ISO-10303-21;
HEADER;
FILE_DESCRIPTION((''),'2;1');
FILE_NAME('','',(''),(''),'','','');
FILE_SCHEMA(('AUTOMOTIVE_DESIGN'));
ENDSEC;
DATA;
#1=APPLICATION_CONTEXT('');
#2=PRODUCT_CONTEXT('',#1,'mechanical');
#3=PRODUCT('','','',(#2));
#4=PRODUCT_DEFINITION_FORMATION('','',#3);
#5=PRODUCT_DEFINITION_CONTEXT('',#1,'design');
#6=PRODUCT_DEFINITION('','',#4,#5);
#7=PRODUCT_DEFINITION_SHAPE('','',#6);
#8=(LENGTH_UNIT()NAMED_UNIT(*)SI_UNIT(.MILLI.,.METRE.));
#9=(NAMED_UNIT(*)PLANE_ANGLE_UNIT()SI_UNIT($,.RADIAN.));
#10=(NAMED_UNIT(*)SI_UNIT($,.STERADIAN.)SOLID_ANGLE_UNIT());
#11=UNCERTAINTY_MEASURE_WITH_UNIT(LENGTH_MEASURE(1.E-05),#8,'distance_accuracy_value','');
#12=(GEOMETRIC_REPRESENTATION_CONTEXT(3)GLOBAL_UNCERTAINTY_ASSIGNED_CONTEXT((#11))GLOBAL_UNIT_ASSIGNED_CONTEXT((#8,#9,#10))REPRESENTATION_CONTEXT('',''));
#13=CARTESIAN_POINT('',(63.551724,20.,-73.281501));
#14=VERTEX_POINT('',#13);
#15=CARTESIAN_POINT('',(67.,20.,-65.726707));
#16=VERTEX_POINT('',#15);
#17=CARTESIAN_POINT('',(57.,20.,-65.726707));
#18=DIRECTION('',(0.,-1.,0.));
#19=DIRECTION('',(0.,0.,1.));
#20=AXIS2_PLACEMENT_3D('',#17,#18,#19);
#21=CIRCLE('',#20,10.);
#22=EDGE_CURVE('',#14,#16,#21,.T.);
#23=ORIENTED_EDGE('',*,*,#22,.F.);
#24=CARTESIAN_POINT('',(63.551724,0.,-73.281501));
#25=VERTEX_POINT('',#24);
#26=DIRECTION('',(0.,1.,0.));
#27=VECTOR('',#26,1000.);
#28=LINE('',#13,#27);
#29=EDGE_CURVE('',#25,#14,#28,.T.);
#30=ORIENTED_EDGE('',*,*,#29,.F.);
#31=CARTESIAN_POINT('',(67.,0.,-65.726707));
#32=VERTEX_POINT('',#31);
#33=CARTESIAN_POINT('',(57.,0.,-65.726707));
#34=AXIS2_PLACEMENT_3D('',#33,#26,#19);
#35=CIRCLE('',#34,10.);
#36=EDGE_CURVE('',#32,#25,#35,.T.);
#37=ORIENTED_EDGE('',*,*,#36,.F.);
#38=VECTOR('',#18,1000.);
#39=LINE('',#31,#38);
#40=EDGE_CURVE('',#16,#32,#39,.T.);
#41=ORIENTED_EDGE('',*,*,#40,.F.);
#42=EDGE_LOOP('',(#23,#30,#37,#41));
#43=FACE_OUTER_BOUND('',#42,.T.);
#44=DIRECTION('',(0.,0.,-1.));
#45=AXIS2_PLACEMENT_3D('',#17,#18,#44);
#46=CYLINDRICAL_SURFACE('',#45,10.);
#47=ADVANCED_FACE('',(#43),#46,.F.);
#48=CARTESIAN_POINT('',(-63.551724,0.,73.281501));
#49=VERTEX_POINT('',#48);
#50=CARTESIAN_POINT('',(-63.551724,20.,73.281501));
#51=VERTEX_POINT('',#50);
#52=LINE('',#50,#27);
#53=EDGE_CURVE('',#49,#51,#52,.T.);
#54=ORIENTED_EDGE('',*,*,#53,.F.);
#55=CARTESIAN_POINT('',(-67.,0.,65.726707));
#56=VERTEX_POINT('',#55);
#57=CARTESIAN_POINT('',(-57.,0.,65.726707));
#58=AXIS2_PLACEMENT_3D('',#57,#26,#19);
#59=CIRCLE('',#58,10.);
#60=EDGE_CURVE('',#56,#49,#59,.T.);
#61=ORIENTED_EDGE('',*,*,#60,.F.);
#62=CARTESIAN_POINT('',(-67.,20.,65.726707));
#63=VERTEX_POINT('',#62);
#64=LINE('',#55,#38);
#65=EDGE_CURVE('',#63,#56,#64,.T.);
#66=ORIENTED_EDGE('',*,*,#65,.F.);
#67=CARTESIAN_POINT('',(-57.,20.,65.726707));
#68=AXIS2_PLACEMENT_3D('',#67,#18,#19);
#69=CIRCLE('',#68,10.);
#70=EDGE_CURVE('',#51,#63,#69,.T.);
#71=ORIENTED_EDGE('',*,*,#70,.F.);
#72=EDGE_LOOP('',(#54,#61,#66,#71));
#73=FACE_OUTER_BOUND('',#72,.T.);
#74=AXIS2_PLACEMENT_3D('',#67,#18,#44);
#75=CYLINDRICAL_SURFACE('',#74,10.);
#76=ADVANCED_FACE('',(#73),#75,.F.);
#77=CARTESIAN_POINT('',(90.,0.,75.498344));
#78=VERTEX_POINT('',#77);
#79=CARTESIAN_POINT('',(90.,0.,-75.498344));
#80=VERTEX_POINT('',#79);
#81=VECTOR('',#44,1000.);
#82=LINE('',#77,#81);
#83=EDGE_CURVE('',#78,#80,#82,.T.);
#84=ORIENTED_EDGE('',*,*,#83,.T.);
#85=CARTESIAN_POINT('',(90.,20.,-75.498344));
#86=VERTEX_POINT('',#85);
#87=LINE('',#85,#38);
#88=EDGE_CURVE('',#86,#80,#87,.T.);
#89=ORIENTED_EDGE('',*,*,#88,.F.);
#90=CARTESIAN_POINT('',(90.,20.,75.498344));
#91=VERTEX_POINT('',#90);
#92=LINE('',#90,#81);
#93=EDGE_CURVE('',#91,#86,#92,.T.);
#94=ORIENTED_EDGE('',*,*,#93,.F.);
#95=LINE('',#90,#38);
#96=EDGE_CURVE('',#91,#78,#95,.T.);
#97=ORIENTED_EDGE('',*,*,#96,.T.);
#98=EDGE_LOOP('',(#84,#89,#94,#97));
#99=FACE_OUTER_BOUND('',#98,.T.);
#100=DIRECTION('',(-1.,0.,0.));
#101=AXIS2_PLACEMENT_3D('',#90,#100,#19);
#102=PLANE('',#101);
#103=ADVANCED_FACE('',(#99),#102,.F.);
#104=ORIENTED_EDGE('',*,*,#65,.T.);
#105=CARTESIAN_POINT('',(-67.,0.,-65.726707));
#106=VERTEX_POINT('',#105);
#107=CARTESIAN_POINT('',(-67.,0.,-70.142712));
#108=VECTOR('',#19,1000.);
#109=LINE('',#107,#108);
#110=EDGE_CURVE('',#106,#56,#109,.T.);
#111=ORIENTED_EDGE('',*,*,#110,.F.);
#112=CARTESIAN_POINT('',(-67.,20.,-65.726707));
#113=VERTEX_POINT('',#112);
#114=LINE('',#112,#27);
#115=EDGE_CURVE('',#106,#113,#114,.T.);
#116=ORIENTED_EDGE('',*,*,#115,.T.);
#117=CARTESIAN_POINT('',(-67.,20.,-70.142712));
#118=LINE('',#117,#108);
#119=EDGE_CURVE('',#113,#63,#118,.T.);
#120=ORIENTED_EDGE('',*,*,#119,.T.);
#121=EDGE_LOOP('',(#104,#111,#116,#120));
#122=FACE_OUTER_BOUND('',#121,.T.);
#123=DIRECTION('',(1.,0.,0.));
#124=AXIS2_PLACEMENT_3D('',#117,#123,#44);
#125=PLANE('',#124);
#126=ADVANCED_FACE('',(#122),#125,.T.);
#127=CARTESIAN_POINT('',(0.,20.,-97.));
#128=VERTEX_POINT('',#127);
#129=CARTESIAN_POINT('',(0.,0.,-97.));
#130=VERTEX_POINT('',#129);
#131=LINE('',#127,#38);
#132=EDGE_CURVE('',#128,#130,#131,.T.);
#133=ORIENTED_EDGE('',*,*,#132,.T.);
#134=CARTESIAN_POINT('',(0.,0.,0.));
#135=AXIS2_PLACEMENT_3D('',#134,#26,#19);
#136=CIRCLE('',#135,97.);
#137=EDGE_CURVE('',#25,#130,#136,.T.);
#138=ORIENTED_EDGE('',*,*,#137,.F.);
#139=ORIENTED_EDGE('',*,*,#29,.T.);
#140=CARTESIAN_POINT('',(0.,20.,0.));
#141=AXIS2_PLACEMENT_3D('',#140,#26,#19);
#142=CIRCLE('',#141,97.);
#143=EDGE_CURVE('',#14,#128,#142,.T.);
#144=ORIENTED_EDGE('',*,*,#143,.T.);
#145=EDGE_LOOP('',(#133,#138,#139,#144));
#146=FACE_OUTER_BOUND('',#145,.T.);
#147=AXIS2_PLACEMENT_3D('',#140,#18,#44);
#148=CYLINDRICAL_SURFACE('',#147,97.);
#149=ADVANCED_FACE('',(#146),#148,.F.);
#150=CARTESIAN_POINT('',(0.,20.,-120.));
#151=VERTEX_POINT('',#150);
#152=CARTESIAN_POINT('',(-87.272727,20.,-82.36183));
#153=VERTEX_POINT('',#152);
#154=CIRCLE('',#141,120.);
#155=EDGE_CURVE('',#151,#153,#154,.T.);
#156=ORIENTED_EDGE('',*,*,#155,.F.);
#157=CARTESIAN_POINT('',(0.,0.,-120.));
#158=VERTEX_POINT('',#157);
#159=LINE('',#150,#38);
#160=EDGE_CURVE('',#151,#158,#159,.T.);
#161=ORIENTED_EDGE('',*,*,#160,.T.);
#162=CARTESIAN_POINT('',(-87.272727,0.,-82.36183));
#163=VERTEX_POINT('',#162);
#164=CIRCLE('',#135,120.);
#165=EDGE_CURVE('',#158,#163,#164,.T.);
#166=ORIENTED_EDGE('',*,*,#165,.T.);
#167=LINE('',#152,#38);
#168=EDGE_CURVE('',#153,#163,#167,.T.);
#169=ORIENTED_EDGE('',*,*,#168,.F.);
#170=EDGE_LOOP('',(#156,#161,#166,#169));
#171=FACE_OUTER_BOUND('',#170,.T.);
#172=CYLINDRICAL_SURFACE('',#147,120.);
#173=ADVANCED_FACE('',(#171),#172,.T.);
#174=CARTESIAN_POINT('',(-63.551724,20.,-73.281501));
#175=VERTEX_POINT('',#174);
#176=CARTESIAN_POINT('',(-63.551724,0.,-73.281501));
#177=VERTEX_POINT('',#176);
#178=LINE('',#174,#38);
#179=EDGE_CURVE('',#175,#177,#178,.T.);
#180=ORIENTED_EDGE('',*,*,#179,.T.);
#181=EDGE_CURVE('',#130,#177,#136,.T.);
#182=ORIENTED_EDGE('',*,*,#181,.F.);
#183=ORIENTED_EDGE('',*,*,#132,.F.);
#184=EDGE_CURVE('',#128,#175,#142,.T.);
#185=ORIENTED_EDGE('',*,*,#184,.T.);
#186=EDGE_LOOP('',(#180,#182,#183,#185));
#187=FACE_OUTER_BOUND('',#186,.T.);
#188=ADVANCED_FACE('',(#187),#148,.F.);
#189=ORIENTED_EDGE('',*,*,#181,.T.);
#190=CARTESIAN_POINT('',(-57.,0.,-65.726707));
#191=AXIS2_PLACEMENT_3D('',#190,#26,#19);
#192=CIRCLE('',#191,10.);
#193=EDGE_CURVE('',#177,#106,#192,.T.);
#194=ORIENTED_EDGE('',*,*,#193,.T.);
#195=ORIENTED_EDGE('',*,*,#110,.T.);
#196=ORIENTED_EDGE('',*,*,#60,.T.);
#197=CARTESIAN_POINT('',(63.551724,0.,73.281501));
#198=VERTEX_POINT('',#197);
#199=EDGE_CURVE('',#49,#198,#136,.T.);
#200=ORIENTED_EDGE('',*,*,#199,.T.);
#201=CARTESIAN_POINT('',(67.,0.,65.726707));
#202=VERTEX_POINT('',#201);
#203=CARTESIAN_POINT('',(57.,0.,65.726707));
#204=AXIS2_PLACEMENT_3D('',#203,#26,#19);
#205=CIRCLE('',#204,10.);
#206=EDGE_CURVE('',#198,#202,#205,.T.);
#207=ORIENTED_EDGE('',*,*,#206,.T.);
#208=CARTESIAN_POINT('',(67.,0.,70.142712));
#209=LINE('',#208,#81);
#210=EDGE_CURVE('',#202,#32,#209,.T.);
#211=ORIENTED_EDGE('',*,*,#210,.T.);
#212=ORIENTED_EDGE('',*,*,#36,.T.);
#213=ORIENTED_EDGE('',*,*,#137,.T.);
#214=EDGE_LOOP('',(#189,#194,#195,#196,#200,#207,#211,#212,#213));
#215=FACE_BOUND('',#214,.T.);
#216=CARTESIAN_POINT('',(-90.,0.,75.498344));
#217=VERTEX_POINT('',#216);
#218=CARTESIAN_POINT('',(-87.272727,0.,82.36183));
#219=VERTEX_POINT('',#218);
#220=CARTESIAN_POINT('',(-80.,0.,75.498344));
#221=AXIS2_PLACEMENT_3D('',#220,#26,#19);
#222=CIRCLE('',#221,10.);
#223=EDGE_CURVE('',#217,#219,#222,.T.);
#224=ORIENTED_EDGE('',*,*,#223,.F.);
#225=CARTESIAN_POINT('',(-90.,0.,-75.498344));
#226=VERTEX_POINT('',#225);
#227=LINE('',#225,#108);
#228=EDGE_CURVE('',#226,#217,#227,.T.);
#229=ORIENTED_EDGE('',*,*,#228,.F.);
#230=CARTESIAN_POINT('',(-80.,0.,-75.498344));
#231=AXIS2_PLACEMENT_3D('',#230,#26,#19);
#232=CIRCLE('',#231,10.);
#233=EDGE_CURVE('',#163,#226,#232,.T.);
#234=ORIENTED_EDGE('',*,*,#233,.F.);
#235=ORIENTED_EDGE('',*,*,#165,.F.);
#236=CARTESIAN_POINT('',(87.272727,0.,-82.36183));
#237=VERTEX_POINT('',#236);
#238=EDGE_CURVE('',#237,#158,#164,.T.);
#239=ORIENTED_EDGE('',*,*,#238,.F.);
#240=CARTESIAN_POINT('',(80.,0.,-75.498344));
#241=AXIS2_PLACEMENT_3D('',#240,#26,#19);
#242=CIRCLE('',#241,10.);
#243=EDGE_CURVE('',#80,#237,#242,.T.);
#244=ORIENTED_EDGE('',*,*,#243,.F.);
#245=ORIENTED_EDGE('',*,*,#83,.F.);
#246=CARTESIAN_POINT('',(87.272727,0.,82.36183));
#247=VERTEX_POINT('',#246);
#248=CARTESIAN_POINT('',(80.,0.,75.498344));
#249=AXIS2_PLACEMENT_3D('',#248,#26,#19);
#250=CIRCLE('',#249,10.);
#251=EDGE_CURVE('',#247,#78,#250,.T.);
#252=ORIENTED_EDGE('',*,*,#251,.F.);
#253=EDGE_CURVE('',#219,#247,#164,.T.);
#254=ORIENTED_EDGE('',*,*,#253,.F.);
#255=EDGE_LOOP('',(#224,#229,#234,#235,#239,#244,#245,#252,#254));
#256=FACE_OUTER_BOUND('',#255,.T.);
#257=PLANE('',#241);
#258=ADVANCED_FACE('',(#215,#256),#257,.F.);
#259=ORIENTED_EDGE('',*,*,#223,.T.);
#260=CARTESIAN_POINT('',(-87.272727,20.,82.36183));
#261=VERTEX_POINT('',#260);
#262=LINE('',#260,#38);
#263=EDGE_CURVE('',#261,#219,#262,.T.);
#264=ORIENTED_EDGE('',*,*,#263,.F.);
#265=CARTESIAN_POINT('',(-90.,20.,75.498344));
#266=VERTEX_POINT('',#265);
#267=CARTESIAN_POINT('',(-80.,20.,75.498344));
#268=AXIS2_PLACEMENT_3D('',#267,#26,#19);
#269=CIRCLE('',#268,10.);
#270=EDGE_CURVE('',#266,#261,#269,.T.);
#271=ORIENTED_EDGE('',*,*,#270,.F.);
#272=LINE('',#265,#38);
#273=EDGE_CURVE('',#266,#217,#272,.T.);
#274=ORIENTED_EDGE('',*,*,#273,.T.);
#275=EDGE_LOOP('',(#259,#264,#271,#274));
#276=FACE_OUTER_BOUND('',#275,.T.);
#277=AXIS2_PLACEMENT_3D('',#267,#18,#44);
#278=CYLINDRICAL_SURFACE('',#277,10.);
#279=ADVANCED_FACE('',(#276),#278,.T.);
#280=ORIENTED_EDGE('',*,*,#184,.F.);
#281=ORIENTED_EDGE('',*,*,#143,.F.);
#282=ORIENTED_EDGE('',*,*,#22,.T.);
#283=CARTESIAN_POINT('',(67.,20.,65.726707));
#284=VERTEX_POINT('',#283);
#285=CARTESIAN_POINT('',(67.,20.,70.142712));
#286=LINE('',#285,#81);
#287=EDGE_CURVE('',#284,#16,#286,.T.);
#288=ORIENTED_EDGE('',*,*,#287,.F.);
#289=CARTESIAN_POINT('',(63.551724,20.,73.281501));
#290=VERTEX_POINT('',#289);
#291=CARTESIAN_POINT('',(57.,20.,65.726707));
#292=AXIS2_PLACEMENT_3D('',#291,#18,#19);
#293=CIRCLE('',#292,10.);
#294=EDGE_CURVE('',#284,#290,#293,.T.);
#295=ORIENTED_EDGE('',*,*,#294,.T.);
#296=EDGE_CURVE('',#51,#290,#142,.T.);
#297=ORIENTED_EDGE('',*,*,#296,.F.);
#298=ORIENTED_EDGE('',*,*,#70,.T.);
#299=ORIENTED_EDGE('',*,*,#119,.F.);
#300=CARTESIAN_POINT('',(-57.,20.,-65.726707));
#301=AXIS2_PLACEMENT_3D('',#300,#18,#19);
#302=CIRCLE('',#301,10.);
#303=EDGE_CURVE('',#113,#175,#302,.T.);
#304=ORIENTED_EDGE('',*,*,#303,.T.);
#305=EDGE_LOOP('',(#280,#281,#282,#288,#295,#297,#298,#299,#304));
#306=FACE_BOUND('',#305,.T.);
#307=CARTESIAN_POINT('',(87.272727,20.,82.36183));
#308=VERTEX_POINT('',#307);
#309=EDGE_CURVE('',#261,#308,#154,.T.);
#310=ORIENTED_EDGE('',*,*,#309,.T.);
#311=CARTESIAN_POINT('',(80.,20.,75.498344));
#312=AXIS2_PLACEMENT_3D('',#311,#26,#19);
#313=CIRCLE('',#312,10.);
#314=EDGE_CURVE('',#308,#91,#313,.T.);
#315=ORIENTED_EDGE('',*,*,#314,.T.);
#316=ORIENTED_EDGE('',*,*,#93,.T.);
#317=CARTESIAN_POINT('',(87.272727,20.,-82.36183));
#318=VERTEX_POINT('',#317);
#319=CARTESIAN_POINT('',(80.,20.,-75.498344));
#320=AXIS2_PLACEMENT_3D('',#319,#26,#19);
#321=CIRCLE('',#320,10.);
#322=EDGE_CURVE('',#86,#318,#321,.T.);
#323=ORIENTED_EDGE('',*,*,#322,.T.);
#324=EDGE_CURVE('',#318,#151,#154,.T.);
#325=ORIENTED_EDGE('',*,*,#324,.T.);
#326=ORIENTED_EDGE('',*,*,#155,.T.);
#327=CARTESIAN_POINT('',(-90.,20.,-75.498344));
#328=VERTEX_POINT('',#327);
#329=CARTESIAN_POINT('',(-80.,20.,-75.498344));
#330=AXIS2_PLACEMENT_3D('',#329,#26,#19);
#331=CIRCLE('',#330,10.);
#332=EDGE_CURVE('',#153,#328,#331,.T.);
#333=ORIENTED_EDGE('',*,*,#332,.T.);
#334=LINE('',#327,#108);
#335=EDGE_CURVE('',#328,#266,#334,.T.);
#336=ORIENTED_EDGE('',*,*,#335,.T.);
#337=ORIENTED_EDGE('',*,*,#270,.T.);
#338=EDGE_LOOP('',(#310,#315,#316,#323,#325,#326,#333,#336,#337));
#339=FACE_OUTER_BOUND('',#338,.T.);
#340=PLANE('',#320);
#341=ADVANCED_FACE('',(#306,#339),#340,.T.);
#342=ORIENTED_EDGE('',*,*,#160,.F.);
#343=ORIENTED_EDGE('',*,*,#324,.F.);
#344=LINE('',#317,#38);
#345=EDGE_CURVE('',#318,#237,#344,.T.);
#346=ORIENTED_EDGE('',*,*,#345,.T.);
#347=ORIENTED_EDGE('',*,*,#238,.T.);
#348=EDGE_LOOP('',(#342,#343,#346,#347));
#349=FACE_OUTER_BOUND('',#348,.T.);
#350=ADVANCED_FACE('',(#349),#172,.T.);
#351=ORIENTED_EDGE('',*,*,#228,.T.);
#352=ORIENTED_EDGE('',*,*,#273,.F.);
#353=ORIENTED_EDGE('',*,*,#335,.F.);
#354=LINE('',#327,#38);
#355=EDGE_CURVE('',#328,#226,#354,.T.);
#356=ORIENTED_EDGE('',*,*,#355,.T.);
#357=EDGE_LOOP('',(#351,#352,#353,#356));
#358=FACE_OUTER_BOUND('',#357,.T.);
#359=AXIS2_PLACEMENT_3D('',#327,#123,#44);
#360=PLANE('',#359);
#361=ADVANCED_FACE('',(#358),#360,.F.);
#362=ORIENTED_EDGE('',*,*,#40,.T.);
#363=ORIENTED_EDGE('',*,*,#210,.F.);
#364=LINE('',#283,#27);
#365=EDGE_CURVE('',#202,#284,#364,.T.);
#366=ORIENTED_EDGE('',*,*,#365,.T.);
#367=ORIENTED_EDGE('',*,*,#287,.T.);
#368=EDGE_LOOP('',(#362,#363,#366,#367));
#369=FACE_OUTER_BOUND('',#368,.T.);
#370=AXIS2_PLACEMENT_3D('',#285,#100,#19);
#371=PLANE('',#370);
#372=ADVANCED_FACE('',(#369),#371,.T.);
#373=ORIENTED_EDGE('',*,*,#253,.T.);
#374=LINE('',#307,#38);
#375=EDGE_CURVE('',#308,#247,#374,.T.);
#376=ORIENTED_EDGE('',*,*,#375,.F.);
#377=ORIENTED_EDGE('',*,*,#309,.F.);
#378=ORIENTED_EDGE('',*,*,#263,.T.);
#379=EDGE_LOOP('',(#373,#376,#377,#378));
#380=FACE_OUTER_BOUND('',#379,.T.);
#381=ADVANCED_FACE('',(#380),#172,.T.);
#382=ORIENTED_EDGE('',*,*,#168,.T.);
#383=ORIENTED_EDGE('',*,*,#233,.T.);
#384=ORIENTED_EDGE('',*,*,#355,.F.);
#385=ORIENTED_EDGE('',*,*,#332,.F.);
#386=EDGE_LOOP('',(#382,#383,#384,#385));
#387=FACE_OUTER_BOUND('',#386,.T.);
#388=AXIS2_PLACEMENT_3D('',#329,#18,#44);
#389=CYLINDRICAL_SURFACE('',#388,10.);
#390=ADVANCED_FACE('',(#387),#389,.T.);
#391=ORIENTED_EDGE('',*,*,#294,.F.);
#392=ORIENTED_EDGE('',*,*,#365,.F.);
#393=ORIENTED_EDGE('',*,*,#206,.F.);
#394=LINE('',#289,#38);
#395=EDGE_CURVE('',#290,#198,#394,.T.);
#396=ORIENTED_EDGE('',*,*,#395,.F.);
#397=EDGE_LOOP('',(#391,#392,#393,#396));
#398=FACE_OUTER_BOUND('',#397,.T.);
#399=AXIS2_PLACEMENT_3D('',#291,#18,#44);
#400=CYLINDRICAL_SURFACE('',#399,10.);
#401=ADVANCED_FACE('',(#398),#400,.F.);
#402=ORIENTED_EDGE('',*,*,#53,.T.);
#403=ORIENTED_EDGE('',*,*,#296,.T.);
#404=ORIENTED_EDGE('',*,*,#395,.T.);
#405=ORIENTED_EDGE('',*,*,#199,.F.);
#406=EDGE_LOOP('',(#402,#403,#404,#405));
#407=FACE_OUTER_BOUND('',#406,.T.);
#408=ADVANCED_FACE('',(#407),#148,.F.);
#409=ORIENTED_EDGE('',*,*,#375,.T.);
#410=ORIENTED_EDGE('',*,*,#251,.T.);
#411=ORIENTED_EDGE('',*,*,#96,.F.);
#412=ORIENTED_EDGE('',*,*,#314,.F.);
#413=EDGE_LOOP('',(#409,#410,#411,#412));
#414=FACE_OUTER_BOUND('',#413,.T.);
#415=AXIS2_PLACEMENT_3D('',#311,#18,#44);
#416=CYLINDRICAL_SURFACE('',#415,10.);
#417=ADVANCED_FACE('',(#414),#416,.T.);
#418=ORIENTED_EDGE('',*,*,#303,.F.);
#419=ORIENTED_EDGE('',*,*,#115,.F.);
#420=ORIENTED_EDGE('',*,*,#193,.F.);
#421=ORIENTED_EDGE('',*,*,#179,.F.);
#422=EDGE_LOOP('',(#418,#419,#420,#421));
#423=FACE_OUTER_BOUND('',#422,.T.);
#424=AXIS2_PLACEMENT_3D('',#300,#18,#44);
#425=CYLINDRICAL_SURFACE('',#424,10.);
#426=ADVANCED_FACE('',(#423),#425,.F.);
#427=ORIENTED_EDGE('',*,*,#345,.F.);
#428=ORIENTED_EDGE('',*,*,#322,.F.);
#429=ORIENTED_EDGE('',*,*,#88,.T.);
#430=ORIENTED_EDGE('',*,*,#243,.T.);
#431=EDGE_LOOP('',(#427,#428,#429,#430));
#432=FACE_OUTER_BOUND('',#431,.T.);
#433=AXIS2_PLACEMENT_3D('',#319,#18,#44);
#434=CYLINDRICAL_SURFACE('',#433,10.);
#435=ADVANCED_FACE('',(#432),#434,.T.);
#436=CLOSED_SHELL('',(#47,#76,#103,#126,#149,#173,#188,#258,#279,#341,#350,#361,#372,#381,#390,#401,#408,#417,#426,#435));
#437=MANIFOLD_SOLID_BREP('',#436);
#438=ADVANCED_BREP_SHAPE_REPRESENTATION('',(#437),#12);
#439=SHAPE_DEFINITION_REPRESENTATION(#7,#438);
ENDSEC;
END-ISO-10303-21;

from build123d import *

# Parameters (mm, degrees)
EXTRUDE_1_DEPTH = 20
FILLET_1_R      = 10


with BuildPart() as part:
    # 草图1 → 凸台-拉伸1 (new body)
    with BuildSketch(Plane(origin=(0, 0, 0), x_dir=(1, 0, 0), z_dir=(0, 1, 0))):
        with BuildLine():
            Line((90, -75.498344353), (90, 75.498344353))
            ThreePointArc((90, 75.498344353), (89.293203773, 79.191089082), (87.272727273, 82.361830203))
            ThreePointArc((87.272727273, 82.361830203), (0, 120), (-87.272727273, 82.361830203))
            ThreePointArc((-87.272727273, 82.361830203), (-89.293203773, 79.191089082), (-90, 75.498344353))
            Line((-90, 75.498344353), (-90, -75.498344353))
            ThreePointArc((-90, -75.498344353), (-89.293203773, -79.191089082), (-87.272727273, -82.361830203))
            ThreePointArc((-87.272727273, -82.361830203), (0, -120), (87.272727273, -82.361830203))
            ThreePointArc((87.272727273, -82.361830203), (89.293203773, -79.191089082), (90, -75.498344353))
        make_face()
        with BuildLine():
            Line((67, -70.142711667), (67, 70.142711667))
            ThreePointArc((67, 70.142711667), (0, 97), (-67, 70.142711667))
            Line((-67, 70.142711667), (-67, -70.142711667))
            ThreePointArc((-67, -70.142711667), (0, -97), (67, -70.142711667))
        make_face(mode=Mode.SUBTRACT)
    extrude(amount=EXTRUDE_1_DEPTH)

    # 圆角1
    fillet_1_edges = [part.edges().sort_by_distance(p)[0] for p in [
        (-67, 10, 70.142711667),
        (67, 10, 70.142711667),
        (67, 10, -70.142711667),
        (-67, 10, -70.142711667),
    ]]
    fillet(fillet_1_edges, radius=FILLET_1_R)


solid = part.part
